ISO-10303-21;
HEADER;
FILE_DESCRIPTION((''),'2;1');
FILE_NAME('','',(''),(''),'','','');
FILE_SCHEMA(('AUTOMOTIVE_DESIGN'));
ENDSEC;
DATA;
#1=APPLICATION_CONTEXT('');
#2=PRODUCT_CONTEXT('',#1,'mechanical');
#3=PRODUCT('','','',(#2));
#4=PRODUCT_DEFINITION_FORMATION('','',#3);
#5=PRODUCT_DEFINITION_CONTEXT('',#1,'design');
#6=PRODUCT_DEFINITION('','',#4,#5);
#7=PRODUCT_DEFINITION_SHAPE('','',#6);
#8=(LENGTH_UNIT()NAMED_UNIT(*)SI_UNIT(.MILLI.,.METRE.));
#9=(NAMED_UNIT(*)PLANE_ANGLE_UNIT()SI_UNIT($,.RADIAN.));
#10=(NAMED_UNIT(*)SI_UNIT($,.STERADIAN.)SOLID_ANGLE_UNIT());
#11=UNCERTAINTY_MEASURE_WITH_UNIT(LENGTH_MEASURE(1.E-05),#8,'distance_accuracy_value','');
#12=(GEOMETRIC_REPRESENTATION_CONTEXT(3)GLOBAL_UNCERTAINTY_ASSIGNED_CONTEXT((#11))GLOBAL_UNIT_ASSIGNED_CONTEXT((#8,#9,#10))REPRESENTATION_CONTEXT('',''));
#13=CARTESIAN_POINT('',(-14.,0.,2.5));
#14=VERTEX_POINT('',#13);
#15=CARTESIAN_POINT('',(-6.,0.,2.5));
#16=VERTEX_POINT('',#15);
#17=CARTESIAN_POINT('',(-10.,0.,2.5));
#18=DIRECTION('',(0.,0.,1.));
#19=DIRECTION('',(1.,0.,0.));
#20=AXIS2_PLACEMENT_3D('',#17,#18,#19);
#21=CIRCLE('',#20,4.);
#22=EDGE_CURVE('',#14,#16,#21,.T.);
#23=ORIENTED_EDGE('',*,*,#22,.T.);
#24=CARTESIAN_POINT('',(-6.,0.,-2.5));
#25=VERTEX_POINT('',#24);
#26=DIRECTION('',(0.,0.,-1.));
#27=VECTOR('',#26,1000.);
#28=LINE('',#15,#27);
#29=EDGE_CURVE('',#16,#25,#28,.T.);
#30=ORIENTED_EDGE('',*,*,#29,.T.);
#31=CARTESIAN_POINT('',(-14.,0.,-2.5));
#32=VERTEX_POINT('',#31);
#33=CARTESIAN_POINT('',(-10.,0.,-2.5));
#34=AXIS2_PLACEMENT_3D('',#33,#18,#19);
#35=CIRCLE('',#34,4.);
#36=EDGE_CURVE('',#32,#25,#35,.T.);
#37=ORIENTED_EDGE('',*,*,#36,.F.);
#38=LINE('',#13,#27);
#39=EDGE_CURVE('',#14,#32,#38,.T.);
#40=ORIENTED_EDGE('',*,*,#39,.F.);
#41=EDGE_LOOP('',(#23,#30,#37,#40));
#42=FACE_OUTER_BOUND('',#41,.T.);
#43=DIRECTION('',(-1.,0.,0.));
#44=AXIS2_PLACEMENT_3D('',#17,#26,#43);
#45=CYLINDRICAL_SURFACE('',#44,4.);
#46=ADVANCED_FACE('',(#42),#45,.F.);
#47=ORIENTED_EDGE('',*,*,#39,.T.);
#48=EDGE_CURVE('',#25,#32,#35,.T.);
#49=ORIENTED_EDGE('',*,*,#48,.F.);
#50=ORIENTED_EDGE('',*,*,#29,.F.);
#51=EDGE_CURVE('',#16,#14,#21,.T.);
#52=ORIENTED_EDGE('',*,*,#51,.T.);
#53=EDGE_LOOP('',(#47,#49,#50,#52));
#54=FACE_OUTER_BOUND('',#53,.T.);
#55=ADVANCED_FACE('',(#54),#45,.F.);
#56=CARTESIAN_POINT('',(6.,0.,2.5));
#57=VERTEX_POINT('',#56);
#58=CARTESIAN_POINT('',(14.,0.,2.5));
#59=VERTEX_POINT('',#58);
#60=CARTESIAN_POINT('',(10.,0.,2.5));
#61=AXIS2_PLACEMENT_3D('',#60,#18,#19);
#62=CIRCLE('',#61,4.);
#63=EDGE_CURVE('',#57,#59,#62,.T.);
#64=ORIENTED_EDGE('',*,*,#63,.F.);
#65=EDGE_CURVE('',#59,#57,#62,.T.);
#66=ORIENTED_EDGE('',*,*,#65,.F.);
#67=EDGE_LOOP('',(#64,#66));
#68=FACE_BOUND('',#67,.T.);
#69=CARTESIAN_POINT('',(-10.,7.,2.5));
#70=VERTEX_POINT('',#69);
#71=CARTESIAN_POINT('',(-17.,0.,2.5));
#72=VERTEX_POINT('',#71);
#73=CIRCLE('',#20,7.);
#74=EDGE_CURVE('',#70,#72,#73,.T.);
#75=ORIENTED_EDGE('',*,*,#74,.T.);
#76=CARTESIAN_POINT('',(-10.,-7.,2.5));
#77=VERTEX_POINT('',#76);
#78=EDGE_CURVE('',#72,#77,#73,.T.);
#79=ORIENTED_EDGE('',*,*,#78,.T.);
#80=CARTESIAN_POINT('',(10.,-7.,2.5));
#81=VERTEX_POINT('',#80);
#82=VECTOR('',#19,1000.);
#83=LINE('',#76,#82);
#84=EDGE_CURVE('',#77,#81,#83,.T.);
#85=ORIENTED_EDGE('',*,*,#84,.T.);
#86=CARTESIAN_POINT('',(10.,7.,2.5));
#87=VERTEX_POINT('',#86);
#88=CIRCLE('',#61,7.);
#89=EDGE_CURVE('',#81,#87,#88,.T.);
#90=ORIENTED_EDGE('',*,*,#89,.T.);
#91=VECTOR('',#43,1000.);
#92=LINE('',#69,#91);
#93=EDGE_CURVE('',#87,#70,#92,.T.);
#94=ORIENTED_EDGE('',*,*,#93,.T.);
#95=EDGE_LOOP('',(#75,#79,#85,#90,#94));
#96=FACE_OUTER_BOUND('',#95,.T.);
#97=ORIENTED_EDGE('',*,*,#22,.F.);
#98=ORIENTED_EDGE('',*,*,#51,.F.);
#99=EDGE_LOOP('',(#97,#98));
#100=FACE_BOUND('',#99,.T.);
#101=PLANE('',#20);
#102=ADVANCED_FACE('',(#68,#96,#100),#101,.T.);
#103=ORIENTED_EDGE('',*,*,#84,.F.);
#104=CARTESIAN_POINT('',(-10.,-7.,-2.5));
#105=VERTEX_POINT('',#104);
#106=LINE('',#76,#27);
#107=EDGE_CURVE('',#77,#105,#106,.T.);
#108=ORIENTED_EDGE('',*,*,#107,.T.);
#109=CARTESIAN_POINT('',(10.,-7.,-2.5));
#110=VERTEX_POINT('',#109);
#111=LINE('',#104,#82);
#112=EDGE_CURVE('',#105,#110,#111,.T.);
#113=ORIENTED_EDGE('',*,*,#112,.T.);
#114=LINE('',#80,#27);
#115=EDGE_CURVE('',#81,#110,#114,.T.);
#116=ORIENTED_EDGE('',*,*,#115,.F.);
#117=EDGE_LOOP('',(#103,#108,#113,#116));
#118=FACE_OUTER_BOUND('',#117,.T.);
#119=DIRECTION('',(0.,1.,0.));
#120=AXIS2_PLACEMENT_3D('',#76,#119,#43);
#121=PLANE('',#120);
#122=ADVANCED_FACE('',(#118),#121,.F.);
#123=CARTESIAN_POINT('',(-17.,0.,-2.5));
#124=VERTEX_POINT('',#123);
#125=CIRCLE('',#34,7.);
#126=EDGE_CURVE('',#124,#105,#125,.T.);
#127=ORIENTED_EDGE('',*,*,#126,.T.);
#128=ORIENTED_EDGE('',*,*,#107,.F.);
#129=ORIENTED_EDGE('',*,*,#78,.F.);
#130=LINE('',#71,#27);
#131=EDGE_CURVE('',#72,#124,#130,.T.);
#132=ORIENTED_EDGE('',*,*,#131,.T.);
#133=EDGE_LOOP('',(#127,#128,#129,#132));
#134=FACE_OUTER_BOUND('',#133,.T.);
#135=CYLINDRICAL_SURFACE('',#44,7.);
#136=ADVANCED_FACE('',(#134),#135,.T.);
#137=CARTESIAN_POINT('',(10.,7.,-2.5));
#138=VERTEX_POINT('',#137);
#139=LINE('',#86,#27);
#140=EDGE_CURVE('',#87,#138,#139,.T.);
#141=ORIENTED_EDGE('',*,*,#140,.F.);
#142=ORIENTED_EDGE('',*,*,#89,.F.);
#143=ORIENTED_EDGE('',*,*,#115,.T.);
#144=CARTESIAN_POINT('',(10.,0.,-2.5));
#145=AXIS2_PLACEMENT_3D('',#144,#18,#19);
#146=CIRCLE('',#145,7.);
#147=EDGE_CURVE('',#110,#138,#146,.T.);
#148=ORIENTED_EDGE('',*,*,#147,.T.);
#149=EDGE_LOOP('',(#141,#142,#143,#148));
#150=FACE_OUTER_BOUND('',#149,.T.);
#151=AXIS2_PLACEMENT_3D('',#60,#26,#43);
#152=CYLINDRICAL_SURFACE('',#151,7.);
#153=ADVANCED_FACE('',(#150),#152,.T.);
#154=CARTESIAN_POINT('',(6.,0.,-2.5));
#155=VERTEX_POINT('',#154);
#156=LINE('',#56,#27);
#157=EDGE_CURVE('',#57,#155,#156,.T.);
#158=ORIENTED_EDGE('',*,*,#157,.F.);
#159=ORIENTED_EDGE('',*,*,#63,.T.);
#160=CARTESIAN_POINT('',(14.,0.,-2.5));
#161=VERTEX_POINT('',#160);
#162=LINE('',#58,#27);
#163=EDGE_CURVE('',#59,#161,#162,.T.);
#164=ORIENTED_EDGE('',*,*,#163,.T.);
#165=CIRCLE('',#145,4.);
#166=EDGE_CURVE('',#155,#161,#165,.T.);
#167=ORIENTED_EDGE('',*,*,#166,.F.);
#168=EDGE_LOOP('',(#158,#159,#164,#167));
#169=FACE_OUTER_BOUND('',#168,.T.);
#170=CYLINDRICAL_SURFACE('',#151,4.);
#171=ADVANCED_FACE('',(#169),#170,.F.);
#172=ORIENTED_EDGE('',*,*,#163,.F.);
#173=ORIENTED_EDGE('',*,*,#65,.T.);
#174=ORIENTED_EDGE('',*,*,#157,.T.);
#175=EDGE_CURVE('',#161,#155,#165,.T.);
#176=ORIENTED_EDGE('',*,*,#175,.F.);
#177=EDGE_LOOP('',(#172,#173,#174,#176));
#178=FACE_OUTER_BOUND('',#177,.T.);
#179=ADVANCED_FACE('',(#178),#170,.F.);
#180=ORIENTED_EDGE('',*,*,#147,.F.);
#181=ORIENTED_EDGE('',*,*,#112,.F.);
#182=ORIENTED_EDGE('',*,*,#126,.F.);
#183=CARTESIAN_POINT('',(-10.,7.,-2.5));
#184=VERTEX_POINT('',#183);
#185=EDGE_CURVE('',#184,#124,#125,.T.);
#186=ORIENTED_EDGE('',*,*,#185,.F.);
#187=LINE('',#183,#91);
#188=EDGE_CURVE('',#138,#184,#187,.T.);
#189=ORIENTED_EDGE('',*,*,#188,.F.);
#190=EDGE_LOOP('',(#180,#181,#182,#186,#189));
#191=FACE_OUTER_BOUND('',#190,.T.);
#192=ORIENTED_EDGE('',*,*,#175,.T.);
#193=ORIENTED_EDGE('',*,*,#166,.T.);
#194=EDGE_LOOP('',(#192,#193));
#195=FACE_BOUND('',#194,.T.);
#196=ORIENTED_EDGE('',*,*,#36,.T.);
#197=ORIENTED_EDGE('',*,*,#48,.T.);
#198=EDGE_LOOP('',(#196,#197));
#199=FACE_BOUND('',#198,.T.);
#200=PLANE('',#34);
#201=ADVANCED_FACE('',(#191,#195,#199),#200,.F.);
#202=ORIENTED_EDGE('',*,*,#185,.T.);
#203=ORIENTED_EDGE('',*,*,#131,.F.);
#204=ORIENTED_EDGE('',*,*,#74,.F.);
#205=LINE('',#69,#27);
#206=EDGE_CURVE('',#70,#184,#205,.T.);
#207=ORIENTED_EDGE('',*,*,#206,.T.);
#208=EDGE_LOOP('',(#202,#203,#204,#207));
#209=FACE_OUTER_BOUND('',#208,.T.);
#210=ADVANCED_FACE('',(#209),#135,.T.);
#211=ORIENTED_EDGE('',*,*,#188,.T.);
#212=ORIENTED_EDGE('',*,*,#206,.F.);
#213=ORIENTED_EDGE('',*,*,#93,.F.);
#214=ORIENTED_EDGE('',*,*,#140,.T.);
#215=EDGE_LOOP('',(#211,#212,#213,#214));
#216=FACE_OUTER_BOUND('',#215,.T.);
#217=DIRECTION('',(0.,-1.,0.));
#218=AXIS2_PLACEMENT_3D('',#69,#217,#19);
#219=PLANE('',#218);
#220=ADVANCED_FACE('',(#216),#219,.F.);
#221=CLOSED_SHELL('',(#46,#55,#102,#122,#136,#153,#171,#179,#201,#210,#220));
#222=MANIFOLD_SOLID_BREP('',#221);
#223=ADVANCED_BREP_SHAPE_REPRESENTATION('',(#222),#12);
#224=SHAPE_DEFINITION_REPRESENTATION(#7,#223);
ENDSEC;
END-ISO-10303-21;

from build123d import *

# Parameters (mm, degrees)
LINK_PROFILE_SKETCH_R = 4
LINK_PLATE_5MM_DEPTH  = 2.5


with BuildPart() as part:
    # Link Profile Sketch → Link Plate 5mm (new, symmetric)
    with BuildSketch(Plane.XY):
        with BuildLine():
            Line((-10, 7), (10, 7))
            ThreePointArc((10, 7), (17, 0), (10, -7))
            Line((10, -7), (-10, -7))
            ThreePointArc((-10, -7), (-17, 0), (-10, 7))
        make_face()
        with Locations((-10, 0)):
            Circle(LINK_PROFILE_SKETCH_R, mode=Mode.SUBTRACT)
        with Locations((10, 0)):
            Circle(LINK_PROFILE_SKETCH_R, mode=Mode.SUBTRACT)
    extrude(amount=LINK_PLATE_5MM_DEPTH, both=True)


solid = part.part
